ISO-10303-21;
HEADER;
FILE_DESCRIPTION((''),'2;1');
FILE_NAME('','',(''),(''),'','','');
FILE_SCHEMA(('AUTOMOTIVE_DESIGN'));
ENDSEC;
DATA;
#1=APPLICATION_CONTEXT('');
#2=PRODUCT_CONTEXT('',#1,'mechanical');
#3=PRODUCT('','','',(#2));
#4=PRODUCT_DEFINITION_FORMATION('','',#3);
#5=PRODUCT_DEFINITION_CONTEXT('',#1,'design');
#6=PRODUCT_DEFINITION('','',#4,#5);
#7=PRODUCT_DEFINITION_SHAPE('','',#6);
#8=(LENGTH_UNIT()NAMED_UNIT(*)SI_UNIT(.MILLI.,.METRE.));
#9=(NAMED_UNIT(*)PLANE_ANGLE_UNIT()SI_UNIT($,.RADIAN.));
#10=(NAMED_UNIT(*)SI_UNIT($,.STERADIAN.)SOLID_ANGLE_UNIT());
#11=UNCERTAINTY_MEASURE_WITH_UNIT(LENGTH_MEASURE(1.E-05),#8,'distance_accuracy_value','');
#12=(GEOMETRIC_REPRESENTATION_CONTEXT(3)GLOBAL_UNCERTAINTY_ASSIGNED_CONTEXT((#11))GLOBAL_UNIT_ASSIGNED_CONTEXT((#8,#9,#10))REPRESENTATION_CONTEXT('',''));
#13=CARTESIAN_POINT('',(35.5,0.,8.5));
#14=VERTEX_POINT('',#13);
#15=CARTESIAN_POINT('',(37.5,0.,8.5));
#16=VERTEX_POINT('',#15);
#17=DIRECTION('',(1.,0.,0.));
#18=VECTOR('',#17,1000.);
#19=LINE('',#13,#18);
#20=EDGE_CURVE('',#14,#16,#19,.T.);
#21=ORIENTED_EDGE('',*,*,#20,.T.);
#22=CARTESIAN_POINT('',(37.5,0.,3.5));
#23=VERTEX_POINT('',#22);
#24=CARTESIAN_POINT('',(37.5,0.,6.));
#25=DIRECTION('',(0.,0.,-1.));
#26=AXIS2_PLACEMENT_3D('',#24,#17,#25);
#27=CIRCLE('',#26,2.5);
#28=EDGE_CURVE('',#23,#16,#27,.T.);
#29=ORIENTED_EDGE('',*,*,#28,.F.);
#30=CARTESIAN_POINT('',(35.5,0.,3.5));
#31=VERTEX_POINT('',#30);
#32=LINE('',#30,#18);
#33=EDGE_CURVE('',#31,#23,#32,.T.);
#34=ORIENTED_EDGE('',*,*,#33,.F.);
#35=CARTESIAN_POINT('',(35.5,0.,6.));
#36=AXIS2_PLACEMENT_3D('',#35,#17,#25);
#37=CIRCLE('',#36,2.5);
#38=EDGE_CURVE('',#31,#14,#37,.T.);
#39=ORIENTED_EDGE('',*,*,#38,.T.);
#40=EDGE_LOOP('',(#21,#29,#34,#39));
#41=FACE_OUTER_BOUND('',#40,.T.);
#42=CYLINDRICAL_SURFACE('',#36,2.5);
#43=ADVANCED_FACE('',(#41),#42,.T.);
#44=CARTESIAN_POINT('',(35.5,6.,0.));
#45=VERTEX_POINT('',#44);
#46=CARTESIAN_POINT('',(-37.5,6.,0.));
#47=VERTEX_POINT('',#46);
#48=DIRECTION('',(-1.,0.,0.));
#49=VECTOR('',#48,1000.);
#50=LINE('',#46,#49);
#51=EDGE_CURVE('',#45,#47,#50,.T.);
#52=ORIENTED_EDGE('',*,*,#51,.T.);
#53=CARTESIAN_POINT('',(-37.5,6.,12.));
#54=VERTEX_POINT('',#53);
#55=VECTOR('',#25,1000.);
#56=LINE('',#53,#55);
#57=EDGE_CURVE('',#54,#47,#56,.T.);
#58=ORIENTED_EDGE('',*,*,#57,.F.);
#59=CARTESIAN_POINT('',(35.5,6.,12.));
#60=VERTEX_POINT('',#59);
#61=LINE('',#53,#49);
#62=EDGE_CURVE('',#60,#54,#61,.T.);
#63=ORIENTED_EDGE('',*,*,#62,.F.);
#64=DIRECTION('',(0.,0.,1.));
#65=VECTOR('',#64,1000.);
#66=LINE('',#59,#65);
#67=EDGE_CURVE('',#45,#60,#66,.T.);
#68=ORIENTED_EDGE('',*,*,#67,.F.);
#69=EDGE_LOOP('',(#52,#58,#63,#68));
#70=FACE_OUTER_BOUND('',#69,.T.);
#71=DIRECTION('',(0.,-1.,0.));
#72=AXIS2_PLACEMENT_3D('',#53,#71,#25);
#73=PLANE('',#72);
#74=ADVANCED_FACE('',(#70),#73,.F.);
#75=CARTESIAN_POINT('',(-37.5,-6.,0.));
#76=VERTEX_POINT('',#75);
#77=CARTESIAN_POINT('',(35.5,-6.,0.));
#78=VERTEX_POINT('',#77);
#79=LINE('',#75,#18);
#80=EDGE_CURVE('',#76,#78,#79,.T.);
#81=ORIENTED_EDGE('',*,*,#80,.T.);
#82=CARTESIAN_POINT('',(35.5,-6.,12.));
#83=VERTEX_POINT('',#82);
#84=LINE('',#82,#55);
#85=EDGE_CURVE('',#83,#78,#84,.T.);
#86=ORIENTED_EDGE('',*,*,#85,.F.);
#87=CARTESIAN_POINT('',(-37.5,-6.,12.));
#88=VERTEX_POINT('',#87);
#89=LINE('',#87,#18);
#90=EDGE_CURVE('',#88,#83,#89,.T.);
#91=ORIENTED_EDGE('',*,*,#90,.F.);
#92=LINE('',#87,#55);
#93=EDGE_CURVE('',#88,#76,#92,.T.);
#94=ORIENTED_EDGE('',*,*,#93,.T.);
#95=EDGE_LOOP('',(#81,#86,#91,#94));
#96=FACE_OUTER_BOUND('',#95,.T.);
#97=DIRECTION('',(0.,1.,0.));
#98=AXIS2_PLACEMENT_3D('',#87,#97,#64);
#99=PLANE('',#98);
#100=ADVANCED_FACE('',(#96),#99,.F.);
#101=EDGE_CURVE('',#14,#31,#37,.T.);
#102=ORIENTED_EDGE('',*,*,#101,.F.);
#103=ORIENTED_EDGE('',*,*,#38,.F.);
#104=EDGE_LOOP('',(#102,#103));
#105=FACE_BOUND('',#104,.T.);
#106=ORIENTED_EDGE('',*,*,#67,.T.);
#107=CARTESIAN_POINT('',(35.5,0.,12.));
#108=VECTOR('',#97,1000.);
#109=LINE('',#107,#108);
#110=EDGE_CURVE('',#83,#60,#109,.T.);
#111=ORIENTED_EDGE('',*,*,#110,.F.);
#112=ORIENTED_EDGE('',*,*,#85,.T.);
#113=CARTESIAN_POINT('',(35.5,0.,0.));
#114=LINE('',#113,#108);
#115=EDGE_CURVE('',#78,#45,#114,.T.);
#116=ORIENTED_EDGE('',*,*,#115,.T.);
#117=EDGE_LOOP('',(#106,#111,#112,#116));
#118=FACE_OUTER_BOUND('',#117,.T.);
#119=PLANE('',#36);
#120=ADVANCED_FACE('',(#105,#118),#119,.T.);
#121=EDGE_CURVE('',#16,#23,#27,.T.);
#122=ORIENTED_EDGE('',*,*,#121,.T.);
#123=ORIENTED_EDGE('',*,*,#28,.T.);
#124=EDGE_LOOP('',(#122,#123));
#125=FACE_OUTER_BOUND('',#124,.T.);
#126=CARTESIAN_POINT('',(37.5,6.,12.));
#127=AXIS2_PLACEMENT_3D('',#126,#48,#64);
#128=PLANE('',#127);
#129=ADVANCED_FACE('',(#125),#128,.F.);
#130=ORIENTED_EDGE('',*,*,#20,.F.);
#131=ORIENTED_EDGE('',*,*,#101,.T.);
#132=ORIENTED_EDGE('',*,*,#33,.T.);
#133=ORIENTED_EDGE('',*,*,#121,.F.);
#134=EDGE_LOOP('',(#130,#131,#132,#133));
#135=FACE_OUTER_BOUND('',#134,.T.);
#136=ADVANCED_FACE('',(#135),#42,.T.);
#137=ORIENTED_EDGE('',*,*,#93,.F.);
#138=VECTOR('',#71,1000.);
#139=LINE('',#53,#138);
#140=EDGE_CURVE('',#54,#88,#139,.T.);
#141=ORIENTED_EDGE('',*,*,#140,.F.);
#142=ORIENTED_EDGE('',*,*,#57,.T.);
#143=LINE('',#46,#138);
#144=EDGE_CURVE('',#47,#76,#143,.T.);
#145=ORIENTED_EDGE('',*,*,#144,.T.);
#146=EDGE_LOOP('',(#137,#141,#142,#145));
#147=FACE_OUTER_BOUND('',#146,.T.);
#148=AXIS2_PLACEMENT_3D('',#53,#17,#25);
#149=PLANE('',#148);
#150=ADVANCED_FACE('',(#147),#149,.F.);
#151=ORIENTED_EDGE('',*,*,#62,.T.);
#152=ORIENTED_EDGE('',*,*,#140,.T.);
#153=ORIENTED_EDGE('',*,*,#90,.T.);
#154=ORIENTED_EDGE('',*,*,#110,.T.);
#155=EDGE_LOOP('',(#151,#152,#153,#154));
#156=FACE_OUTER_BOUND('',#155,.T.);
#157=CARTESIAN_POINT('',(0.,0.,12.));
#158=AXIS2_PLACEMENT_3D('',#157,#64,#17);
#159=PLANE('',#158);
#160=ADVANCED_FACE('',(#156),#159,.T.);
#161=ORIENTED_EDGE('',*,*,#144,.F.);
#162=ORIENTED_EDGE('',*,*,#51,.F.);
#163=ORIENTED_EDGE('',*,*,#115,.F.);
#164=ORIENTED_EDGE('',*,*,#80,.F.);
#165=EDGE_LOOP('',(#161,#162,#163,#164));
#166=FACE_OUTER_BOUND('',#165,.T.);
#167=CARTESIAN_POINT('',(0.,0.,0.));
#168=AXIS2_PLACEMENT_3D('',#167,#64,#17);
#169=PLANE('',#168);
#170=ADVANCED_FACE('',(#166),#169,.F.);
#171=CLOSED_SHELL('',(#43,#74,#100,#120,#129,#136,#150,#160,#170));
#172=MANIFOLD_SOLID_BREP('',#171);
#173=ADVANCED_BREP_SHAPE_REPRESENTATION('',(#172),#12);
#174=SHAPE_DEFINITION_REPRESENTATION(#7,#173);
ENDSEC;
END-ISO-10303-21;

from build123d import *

# Parameters (mm, degrees)
SKETCH1_W           = 75
SKETCH1_H           = 12
BOSS_EXTRUDE1_DEPTH = 12
SKETCH2_OUTSIDE_W   = 29.38
SKETCH2_OUTSIDE_H   = 29.38
SKETCH2_OUTSIDE_R   = 2.5
CUT_EXTRUDE1_DEPTH  = 2


with BuildPart() as part:
    # Sketch1 → Boss-Extrude1 (new body)
    with BuildSketch(Plane.XY):
        Rectangle(SKETCH1_W, SKETCH1_H)
    extrude(amount=BOSS_EXTRUDE1_DEPTH)

    # Sketch2 outside → Cut-Extrude1 (cut)
    with BuildSketch(Plane(origin=(37.5, 0, 0), x_dir=(0, 0, -1), z_dir=(1, 0, 0))):
        with Locations((-6, 0)):
            Rectangle(SKETCH2_OUTSIDE_W, SKETCH2_OUTSIDE_H)
        with Locations((-6, 0)):
            Circle(SKETCH2_OUTSIDE_R, mode=Mode.SUBTRACT)
    extrude(amount=-CUT_EXTRUDE1_DEPTH, mode=Mode.SUBTRACT)


solid = part.part
